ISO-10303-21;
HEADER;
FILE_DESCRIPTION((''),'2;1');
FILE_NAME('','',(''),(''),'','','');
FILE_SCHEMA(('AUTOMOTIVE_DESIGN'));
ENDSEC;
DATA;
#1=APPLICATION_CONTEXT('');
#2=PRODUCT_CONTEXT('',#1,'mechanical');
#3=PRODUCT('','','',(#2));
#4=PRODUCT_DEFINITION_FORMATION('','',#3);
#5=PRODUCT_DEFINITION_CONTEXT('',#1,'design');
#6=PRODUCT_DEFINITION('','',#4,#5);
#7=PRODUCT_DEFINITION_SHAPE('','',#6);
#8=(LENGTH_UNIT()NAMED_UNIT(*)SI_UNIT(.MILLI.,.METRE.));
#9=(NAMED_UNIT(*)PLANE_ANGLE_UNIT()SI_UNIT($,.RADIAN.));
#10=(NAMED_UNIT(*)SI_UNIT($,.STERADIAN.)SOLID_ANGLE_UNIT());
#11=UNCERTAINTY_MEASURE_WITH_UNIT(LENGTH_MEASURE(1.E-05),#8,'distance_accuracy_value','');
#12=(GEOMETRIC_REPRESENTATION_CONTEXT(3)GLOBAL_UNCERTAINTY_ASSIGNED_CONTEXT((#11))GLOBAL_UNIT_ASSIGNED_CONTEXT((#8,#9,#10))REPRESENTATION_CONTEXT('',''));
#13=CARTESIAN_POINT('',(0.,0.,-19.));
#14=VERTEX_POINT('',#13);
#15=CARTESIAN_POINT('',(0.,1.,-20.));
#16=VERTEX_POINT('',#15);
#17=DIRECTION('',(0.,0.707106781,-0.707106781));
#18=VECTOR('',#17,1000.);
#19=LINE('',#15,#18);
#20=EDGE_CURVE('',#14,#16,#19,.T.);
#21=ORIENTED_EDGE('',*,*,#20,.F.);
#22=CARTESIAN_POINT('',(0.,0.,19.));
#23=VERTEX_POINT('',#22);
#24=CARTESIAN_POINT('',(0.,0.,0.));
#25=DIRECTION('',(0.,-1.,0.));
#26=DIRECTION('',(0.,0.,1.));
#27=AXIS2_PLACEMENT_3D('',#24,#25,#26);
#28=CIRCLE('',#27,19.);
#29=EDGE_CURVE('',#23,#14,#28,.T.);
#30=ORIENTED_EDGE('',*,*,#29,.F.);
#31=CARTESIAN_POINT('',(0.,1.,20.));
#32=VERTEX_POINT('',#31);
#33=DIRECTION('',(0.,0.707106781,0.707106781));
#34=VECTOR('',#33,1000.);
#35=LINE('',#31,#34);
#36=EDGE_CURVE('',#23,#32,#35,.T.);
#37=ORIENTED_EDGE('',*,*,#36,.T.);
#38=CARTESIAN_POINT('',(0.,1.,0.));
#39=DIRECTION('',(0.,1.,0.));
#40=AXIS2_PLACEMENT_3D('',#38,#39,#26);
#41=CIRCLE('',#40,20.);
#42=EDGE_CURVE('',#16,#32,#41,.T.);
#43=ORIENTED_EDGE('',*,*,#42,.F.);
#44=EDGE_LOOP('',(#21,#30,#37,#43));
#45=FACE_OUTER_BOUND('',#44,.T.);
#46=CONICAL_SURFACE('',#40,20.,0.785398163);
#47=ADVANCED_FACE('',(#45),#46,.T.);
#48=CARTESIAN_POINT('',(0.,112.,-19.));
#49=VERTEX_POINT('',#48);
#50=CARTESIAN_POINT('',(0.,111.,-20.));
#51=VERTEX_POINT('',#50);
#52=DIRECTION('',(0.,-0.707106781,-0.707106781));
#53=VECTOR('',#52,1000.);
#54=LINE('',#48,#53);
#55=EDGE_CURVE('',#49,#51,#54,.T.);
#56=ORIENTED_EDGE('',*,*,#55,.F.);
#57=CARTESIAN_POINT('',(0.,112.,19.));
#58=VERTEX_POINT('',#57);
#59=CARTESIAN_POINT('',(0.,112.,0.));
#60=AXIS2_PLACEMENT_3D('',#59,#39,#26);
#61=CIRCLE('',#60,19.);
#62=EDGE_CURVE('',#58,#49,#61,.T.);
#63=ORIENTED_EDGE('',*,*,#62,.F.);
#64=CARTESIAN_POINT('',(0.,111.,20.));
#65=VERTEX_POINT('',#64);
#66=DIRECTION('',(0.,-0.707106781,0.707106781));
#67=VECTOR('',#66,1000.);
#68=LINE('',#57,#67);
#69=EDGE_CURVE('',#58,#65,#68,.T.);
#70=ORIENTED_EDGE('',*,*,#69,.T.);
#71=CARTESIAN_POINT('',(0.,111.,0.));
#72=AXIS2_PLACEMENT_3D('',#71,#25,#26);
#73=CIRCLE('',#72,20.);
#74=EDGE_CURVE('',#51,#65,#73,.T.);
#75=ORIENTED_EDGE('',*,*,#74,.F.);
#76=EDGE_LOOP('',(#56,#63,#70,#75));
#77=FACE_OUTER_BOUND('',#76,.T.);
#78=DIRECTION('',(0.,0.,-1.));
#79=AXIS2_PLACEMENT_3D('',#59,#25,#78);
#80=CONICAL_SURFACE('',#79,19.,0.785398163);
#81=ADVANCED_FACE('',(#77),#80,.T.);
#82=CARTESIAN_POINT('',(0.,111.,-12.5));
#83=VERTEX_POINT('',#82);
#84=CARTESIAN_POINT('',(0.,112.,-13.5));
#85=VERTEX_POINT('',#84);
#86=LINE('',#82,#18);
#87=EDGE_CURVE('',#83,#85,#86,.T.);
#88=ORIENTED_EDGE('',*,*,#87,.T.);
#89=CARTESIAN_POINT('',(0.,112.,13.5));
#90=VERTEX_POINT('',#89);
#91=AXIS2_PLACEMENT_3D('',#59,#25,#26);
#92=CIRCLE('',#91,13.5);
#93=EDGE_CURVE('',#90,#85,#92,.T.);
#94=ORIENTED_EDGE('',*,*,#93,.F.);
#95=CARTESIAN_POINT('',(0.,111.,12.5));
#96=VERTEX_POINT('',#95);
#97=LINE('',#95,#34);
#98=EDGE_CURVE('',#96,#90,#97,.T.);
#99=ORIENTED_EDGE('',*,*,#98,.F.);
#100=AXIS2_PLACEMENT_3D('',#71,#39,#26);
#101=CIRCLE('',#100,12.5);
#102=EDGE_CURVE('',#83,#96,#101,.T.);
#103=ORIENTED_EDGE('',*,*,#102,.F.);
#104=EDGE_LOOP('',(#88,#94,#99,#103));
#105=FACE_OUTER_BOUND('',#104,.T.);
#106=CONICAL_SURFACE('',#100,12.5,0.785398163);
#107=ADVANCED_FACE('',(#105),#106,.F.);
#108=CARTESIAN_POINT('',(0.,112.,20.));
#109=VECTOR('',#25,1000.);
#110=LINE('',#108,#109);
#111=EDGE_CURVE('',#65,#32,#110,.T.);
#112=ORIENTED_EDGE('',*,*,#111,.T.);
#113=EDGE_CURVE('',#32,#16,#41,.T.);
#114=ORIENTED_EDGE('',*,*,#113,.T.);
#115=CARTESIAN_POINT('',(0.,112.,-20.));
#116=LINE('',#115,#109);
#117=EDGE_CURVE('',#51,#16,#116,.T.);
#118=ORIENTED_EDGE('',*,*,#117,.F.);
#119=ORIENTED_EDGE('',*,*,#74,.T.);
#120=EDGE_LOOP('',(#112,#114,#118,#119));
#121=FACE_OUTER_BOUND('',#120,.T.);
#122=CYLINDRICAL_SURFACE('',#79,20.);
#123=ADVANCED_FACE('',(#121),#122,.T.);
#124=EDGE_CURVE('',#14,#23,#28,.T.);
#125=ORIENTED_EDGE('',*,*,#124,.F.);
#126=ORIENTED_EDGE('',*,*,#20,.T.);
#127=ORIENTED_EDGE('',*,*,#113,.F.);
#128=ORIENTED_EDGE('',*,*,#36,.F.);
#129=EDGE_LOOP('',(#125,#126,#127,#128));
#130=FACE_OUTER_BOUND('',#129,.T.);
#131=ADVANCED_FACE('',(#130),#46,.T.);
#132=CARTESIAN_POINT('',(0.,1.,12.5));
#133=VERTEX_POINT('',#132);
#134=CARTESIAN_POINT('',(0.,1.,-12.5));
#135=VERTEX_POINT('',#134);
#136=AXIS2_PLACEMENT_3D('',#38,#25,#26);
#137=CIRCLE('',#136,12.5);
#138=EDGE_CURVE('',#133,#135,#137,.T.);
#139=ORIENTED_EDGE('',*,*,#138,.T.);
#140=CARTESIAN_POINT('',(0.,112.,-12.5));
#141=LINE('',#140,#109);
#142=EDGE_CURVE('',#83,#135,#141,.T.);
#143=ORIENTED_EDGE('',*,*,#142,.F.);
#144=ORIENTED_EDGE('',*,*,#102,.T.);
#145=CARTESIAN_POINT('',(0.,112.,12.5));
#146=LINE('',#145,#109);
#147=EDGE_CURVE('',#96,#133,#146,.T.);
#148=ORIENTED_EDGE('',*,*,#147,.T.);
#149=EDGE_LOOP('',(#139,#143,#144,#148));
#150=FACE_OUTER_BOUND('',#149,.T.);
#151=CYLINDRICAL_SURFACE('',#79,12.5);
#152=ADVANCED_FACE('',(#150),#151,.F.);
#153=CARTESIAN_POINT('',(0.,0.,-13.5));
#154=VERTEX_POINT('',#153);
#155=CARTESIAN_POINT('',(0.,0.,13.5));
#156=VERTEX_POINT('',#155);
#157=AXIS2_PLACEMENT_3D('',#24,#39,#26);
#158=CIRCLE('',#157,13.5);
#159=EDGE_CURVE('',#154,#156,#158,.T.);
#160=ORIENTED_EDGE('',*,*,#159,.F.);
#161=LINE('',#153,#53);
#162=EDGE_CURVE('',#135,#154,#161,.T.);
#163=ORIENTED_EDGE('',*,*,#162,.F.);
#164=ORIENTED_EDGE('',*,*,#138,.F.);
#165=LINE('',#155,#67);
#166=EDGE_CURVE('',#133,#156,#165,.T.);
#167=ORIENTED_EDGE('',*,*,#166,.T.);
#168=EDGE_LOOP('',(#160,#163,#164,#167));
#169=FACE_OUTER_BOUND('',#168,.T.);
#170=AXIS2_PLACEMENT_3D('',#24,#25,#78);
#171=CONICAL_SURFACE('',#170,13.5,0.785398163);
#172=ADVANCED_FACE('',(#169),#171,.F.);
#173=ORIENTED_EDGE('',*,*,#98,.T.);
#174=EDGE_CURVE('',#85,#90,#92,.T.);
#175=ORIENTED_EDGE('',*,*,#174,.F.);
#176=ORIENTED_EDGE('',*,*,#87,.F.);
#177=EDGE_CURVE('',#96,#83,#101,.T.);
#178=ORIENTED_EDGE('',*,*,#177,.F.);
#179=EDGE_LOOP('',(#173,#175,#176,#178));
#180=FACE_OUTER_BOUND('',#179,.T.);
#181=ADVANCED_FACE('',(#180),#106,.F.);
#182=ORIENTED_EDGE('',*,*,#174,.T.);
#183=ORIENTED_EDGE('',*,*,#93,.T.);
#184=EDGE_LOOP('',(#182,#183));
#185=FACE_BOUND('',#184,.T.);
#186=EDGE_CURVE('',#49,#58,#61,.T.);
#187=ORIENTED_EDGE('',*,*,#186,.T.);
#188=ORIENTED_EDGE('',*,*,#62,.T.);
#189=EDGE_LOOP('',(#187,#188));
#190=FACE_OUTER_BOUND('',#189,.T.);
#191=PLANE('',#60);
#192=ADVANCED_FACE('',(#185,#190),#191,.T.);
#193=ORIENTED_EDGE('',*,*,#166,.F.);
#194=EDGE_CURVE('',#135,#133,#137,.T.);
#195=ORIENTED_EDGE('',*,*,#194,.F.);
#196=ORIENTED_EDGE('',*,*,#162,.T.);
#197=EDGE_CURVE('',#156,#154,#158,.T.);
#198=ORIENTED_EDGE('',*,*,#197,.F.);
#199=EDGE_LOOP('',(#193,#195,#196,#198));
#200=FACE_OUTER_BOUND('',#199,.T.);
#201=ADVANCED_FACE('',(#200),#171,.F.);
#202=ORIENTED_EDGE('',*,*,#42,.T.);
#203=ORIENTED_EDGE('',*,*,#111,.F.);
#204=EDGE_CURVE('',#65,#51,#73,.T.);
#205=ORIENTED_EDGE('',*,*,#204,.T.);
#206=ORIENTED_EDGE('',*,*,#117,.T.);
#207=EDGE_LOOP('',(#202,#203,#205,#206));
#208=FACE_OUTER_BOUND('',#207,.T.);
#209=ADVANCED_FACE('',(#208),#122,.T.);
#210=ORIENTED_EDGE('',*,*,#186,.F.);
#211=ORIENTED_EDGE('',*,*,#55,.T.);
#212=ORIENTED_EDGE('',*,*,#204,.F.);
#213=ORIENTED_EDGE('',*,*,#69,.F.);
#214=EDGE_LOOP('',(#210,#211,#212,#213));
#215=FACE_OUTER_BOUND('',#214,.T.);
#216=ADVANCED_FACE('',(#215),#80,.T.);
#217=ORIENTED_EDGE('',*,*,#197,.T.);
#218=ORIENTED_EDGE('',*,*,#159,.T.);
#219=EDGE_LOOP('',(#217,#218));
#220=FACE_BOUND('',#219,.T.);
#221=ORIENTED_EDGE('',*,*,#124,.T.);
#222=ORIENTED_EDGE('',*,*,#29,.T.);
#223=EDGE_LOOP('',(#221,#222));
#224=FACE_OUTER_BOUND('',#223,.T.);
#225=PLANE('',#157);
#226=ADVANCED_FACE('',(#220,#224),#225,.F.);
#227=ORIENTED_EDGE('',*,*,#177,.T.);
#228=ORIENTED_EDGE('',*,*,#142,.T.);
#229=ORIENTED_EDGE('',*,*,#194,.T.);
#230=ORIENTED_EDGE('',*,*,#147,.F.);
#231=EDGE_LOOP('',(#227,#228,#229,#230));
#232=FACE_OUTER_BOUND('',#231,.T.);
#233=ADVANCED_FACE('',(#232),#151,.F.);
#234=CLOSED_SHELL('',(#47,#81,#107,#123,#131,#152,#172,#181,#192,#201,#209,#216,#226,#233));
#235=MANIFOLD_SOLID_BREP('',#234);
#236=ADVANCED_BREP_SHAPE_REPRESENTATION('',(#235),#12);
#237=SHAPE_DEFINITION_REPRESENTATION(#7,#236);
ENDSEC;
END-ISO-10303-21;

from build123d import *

# Parameters (mm, degrees)
SKETCH1_R           = 20
SKETCH1_R_2         = 12.5
BOSS_EXTRUDE1_DEPTH = 112
CHAMFER1_SIZE       = 1


with BuildPart() as part:
    # Sketch1 → Boss-Extrude1 (new body)
    with BuildSketch(Plane(origin=(0, 0, 0), x_dir=(1, 0, 0), z_dir=(0, 1, 0))):
        with Locations(Location((0, 0, 0), (0, 0, 270))):
            Circle(SKETCH1_R)
        with Locations(Location((0, 0, 0), (0, 0, 270))):
            Circle(SKETCH1_R_2, mode=Mode.SUBTRACT)
    extrude(amount=BOSS_EXTRUDE1_DEPTH)

    # Chamfer1
    chamfer1_edges = [part.edges().sort_by_distance(p)[0] for p in [
        (0, 0, -20),
        (0, 112, -20),
        (0, 0, -12.5),
        (0, 112, -12.5),
    ]]
    chamfer(chamfer1_edges, length=CHAMFER1_SIZE)


solid = part.part
